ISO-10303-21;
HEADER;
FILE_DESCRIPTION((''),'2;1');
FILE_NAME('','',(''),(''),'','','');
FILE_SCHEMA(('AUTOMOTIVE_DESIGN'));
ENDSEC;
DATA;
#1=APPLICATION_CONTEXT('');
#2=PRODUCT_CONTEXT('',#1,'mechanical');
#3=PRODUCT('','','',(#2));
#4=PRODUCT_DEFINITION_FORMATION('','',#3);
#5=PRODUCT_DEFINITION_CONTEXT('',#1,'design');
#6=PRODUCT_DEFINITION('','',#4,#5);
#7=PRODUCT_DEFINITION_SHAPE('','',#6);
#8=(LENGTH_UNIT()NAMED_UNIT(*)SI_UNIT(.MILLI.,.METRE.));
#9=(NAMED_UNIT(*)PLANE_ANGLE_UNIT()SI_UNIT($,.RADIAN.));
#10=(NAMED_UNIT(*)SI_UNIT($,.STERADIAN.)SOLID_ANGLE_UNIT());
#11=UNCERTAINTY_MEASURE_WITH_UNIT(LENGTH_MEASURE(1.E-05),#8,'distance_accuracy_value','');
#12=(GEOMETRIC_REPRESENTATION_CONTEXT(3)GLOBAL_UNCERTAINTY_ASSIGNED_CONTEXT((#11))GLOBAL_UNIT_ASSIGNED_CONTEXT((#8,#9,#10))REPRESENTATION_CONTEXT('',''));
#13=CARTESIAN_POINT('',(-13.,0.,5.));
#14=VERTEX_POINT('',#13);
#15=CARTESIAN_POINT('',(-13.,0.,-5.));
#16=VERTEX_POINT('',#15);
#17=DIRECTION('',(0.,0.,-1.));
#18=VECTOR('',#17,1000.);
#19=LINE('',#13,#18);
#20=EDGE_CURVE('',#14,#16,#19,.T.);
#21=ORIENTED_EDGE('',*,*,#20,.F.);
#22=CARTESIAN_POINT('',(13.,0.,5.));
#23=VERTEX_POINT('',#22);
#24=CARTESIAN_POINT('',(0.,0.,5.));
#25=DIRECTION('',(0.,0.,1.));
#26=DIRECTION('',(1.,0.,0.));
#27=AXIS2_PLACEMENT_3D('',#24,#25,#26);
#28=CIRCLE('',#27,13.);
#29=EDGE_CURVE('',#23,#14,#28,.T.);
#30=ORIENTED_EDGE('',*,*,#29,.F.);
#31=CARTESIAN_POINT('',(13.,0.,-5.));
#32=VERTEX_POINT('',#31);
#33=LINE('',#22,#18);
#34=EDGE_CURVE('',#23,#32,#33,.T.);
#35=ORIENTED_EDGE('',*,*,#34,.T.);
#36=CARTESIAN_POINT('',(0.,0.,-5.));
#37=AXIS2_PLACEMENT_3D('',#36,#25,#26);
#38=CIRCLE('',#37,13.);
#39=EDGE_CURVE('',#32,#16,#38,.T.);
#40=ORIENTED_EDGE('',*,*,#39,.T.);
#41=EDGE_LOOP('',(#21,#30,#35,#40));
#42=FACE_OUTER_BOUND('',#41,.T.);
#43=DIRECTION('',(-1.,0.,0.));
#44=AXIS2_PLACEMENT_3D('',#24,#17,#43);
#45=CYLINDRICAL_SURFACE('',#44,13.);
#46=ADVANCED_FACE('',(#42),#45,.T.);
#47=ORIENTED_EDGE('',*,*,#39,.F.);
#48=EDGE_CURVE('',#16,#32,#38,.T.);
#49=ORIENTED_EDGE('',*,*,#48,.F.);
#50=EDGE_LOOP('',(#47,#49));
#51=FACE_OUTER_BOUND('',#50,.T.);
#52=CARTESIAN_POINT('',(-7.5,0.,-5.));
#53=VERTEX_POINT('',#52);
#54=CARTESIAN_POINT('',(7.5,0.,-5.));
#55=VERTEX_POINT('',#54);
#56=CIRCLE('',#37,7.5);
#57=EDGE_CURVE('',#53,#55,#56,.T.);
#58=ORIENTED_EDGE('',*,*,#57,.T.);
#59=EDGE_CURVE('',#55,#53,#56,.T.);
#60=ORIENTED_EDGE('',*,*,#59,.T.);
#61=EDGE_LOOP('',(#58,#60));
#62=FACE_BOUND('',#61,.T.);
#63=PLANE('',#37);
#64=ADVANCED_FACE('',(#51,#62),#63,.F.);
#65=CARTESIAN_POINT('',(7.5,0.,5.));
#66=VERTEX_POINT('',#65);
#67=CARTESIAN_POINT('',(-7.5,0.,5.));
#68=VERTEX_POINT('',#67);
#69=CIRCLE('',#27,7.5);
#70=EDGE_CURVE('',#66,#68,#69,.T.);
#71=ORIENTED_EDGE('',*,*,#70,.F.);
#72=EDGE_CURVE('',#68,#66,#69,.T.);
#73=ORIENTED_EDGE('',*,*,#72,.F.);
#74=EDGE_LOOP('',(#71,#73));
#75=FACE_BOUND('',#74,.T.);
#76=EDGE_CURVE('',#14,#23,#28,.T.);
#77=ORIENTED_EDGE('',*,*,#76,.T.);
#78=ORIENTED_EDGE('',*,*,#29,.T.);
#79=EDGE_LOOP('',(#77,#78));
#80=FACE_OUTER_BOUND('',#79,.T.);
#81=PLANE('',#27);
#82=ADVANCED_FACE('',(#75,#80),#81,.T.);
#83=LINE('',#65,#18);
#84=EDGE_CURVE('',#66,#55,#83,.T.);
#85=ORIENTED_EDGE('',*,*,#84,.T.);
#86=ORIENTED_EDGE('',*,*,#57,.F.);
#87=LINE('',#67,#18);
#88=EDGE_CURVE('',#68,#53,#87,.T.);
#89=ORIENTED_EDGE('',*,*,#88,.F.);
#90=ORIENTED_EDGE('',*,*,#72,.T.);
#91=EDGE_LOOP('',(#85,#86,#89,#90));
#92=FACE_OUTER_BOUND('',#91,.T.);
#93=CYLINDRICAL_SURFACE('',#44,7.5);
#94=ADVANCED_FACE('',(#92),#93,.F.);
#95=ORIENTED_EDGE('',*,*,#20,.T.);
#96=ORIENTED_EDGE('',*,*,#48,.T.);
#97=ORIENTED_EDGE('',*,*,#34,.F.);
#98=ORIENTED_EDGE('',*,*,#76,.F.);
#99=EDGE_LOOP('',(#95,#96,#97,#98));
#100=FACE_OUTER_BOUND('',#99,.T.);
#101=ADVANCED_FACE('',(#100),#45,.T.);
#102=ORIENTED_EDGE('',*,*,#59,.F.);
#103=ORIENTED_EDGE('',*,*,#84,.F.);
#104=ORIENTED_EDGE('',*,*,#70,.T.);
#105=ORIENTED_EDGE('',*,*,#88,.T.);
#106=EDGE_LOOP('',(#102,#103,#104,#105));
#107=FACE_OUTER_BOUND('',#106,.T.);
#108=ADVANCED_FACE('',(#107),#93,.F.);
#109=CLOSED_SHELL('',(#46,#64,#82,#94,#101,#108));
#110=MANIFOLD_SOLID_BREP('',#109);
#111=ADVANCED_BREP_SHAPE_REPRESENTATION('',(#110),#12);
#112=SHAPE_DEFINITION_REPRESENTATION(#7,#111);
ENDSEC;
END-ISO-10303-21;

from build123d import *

# Parameters (mm, degrees)
SKETCH_1_R      = 13
SKETCH_1_R_2    = 7.5
EXTRUDE_1_DEPTH = 5


with BuildPart() as part:
    # 草图1 → 凸台-拉伸1 (new, symmetric)
    with BuildSketch(Plane.XY):
        Circle(SKETCH_1_R)
        Circle(SKETCH_1_R_2, mode=Mode.SUBTRACT)
    extrude(amount=EXTRUDE_1_DEPTH, both=True)


solid = part.part
